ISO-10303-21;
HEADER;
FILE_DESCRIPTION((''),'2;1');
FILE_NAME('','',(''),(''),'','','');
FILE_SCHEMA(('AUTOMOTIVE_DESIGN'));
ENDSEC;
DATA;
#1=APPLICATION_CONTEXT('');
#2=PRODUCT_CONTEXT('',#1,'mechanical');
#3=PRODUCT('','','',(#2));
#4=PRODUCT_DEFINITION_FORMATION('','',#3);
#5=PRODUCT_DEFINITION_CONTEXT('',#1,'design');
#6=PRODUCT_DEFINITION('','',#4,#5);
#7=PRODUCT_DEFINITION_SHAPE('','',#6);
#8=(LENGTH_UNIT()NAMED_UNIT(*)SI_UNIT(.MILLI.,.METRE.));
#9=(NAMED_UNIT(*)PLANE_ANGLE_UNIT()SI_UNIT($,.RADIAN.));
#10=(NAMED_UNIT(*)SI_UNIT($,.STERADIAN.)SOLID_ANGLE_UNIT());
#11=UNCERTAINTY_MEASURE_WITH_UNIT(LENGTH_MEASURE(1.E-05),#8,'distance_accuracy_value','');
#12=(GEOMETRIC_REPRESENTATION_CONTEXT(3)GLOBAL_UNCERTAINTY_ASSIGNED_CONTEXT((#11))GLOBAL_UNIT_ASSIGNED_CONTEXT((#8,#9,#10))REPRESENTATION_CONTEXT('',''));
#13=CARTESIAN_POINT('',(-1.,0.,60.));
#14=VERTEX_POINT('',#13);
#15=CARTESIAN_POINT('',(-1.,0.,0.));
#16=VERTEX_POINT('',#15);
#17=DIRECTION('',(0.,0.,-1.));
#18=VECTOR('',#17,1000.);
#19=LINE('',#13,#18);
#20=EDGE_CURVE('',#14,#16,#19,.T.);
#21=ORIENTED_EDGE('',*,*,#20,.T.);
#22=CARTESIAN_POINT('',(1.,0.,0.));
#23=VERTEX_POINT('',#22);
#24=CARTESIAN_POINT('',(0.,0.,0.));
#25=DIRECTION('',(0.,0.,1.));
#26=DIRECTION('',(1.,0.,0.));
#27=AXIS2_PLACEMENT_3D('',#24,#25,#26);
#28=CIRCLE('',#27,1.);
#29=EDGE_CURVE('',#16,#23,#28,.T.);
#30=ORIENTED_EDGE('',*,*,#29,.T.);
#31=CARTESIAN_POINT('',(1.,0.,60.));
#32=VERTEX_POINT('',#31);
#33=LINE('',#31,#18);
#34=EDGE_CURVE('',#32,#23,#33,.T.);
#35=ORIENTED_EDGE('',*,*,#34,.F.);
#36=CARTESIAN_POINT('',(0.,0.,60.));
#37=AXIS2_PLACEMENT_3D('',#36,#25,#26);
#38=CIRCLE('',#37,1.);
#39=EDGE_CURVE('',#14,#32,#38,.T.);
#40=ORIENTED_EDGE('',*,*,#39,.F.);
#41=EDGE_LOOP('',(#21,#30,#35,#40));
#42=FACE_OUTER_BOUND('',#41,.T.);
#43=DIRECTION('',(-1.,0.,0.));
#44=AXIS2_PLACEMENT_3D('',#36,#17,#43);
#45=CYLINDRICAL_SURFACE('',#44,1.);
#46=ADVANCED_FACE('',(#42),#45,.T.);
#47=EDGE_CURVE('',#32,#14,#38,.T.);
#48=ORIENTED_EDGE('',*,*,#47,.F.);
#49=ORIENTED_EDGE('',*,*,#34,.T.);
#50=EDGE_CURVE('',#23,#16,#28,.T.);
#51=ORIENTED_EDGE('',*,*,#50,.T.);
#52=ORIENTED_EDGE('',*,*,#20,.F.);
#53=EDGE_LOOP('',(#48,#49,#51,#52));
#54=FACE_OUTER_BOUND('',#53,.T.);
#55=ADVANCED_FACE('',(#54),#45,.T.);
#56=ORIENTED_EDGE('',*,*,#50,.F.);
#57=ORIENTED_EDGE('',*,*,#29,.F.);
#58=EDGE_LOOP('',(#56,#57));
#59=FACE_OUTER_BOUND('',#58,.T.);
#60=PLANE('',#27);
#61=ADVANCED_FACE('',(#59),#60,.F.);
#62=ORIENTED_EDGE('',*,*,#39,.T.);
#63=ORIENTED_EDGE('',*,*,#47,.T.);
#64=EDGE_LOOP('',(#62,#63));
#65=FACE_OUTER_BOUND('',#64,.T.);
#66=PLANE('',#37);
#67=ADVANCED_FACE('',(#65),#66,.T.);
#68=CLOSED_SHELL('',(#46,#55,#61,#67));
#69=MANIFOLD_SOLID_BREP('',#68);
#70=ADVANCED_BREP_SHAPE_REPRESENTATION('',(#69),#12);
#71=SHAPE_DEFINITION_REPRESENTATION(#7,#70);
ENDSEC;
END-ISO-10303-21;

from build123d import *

# Parameters (mm, degrees)
SKETCH1_R           = 1
BOSS_EXTRUDE1_DEPTH = 60


with BuildPart() as part:
    # Sketch1 → Boss-Extrude1 (new body)
    with BuildSketch(Plane.XY):
        Circle(SKETCH1_R)
    extrude(amount=BOSS_EXTRUDE1_DEPTH)


solid = part.part
